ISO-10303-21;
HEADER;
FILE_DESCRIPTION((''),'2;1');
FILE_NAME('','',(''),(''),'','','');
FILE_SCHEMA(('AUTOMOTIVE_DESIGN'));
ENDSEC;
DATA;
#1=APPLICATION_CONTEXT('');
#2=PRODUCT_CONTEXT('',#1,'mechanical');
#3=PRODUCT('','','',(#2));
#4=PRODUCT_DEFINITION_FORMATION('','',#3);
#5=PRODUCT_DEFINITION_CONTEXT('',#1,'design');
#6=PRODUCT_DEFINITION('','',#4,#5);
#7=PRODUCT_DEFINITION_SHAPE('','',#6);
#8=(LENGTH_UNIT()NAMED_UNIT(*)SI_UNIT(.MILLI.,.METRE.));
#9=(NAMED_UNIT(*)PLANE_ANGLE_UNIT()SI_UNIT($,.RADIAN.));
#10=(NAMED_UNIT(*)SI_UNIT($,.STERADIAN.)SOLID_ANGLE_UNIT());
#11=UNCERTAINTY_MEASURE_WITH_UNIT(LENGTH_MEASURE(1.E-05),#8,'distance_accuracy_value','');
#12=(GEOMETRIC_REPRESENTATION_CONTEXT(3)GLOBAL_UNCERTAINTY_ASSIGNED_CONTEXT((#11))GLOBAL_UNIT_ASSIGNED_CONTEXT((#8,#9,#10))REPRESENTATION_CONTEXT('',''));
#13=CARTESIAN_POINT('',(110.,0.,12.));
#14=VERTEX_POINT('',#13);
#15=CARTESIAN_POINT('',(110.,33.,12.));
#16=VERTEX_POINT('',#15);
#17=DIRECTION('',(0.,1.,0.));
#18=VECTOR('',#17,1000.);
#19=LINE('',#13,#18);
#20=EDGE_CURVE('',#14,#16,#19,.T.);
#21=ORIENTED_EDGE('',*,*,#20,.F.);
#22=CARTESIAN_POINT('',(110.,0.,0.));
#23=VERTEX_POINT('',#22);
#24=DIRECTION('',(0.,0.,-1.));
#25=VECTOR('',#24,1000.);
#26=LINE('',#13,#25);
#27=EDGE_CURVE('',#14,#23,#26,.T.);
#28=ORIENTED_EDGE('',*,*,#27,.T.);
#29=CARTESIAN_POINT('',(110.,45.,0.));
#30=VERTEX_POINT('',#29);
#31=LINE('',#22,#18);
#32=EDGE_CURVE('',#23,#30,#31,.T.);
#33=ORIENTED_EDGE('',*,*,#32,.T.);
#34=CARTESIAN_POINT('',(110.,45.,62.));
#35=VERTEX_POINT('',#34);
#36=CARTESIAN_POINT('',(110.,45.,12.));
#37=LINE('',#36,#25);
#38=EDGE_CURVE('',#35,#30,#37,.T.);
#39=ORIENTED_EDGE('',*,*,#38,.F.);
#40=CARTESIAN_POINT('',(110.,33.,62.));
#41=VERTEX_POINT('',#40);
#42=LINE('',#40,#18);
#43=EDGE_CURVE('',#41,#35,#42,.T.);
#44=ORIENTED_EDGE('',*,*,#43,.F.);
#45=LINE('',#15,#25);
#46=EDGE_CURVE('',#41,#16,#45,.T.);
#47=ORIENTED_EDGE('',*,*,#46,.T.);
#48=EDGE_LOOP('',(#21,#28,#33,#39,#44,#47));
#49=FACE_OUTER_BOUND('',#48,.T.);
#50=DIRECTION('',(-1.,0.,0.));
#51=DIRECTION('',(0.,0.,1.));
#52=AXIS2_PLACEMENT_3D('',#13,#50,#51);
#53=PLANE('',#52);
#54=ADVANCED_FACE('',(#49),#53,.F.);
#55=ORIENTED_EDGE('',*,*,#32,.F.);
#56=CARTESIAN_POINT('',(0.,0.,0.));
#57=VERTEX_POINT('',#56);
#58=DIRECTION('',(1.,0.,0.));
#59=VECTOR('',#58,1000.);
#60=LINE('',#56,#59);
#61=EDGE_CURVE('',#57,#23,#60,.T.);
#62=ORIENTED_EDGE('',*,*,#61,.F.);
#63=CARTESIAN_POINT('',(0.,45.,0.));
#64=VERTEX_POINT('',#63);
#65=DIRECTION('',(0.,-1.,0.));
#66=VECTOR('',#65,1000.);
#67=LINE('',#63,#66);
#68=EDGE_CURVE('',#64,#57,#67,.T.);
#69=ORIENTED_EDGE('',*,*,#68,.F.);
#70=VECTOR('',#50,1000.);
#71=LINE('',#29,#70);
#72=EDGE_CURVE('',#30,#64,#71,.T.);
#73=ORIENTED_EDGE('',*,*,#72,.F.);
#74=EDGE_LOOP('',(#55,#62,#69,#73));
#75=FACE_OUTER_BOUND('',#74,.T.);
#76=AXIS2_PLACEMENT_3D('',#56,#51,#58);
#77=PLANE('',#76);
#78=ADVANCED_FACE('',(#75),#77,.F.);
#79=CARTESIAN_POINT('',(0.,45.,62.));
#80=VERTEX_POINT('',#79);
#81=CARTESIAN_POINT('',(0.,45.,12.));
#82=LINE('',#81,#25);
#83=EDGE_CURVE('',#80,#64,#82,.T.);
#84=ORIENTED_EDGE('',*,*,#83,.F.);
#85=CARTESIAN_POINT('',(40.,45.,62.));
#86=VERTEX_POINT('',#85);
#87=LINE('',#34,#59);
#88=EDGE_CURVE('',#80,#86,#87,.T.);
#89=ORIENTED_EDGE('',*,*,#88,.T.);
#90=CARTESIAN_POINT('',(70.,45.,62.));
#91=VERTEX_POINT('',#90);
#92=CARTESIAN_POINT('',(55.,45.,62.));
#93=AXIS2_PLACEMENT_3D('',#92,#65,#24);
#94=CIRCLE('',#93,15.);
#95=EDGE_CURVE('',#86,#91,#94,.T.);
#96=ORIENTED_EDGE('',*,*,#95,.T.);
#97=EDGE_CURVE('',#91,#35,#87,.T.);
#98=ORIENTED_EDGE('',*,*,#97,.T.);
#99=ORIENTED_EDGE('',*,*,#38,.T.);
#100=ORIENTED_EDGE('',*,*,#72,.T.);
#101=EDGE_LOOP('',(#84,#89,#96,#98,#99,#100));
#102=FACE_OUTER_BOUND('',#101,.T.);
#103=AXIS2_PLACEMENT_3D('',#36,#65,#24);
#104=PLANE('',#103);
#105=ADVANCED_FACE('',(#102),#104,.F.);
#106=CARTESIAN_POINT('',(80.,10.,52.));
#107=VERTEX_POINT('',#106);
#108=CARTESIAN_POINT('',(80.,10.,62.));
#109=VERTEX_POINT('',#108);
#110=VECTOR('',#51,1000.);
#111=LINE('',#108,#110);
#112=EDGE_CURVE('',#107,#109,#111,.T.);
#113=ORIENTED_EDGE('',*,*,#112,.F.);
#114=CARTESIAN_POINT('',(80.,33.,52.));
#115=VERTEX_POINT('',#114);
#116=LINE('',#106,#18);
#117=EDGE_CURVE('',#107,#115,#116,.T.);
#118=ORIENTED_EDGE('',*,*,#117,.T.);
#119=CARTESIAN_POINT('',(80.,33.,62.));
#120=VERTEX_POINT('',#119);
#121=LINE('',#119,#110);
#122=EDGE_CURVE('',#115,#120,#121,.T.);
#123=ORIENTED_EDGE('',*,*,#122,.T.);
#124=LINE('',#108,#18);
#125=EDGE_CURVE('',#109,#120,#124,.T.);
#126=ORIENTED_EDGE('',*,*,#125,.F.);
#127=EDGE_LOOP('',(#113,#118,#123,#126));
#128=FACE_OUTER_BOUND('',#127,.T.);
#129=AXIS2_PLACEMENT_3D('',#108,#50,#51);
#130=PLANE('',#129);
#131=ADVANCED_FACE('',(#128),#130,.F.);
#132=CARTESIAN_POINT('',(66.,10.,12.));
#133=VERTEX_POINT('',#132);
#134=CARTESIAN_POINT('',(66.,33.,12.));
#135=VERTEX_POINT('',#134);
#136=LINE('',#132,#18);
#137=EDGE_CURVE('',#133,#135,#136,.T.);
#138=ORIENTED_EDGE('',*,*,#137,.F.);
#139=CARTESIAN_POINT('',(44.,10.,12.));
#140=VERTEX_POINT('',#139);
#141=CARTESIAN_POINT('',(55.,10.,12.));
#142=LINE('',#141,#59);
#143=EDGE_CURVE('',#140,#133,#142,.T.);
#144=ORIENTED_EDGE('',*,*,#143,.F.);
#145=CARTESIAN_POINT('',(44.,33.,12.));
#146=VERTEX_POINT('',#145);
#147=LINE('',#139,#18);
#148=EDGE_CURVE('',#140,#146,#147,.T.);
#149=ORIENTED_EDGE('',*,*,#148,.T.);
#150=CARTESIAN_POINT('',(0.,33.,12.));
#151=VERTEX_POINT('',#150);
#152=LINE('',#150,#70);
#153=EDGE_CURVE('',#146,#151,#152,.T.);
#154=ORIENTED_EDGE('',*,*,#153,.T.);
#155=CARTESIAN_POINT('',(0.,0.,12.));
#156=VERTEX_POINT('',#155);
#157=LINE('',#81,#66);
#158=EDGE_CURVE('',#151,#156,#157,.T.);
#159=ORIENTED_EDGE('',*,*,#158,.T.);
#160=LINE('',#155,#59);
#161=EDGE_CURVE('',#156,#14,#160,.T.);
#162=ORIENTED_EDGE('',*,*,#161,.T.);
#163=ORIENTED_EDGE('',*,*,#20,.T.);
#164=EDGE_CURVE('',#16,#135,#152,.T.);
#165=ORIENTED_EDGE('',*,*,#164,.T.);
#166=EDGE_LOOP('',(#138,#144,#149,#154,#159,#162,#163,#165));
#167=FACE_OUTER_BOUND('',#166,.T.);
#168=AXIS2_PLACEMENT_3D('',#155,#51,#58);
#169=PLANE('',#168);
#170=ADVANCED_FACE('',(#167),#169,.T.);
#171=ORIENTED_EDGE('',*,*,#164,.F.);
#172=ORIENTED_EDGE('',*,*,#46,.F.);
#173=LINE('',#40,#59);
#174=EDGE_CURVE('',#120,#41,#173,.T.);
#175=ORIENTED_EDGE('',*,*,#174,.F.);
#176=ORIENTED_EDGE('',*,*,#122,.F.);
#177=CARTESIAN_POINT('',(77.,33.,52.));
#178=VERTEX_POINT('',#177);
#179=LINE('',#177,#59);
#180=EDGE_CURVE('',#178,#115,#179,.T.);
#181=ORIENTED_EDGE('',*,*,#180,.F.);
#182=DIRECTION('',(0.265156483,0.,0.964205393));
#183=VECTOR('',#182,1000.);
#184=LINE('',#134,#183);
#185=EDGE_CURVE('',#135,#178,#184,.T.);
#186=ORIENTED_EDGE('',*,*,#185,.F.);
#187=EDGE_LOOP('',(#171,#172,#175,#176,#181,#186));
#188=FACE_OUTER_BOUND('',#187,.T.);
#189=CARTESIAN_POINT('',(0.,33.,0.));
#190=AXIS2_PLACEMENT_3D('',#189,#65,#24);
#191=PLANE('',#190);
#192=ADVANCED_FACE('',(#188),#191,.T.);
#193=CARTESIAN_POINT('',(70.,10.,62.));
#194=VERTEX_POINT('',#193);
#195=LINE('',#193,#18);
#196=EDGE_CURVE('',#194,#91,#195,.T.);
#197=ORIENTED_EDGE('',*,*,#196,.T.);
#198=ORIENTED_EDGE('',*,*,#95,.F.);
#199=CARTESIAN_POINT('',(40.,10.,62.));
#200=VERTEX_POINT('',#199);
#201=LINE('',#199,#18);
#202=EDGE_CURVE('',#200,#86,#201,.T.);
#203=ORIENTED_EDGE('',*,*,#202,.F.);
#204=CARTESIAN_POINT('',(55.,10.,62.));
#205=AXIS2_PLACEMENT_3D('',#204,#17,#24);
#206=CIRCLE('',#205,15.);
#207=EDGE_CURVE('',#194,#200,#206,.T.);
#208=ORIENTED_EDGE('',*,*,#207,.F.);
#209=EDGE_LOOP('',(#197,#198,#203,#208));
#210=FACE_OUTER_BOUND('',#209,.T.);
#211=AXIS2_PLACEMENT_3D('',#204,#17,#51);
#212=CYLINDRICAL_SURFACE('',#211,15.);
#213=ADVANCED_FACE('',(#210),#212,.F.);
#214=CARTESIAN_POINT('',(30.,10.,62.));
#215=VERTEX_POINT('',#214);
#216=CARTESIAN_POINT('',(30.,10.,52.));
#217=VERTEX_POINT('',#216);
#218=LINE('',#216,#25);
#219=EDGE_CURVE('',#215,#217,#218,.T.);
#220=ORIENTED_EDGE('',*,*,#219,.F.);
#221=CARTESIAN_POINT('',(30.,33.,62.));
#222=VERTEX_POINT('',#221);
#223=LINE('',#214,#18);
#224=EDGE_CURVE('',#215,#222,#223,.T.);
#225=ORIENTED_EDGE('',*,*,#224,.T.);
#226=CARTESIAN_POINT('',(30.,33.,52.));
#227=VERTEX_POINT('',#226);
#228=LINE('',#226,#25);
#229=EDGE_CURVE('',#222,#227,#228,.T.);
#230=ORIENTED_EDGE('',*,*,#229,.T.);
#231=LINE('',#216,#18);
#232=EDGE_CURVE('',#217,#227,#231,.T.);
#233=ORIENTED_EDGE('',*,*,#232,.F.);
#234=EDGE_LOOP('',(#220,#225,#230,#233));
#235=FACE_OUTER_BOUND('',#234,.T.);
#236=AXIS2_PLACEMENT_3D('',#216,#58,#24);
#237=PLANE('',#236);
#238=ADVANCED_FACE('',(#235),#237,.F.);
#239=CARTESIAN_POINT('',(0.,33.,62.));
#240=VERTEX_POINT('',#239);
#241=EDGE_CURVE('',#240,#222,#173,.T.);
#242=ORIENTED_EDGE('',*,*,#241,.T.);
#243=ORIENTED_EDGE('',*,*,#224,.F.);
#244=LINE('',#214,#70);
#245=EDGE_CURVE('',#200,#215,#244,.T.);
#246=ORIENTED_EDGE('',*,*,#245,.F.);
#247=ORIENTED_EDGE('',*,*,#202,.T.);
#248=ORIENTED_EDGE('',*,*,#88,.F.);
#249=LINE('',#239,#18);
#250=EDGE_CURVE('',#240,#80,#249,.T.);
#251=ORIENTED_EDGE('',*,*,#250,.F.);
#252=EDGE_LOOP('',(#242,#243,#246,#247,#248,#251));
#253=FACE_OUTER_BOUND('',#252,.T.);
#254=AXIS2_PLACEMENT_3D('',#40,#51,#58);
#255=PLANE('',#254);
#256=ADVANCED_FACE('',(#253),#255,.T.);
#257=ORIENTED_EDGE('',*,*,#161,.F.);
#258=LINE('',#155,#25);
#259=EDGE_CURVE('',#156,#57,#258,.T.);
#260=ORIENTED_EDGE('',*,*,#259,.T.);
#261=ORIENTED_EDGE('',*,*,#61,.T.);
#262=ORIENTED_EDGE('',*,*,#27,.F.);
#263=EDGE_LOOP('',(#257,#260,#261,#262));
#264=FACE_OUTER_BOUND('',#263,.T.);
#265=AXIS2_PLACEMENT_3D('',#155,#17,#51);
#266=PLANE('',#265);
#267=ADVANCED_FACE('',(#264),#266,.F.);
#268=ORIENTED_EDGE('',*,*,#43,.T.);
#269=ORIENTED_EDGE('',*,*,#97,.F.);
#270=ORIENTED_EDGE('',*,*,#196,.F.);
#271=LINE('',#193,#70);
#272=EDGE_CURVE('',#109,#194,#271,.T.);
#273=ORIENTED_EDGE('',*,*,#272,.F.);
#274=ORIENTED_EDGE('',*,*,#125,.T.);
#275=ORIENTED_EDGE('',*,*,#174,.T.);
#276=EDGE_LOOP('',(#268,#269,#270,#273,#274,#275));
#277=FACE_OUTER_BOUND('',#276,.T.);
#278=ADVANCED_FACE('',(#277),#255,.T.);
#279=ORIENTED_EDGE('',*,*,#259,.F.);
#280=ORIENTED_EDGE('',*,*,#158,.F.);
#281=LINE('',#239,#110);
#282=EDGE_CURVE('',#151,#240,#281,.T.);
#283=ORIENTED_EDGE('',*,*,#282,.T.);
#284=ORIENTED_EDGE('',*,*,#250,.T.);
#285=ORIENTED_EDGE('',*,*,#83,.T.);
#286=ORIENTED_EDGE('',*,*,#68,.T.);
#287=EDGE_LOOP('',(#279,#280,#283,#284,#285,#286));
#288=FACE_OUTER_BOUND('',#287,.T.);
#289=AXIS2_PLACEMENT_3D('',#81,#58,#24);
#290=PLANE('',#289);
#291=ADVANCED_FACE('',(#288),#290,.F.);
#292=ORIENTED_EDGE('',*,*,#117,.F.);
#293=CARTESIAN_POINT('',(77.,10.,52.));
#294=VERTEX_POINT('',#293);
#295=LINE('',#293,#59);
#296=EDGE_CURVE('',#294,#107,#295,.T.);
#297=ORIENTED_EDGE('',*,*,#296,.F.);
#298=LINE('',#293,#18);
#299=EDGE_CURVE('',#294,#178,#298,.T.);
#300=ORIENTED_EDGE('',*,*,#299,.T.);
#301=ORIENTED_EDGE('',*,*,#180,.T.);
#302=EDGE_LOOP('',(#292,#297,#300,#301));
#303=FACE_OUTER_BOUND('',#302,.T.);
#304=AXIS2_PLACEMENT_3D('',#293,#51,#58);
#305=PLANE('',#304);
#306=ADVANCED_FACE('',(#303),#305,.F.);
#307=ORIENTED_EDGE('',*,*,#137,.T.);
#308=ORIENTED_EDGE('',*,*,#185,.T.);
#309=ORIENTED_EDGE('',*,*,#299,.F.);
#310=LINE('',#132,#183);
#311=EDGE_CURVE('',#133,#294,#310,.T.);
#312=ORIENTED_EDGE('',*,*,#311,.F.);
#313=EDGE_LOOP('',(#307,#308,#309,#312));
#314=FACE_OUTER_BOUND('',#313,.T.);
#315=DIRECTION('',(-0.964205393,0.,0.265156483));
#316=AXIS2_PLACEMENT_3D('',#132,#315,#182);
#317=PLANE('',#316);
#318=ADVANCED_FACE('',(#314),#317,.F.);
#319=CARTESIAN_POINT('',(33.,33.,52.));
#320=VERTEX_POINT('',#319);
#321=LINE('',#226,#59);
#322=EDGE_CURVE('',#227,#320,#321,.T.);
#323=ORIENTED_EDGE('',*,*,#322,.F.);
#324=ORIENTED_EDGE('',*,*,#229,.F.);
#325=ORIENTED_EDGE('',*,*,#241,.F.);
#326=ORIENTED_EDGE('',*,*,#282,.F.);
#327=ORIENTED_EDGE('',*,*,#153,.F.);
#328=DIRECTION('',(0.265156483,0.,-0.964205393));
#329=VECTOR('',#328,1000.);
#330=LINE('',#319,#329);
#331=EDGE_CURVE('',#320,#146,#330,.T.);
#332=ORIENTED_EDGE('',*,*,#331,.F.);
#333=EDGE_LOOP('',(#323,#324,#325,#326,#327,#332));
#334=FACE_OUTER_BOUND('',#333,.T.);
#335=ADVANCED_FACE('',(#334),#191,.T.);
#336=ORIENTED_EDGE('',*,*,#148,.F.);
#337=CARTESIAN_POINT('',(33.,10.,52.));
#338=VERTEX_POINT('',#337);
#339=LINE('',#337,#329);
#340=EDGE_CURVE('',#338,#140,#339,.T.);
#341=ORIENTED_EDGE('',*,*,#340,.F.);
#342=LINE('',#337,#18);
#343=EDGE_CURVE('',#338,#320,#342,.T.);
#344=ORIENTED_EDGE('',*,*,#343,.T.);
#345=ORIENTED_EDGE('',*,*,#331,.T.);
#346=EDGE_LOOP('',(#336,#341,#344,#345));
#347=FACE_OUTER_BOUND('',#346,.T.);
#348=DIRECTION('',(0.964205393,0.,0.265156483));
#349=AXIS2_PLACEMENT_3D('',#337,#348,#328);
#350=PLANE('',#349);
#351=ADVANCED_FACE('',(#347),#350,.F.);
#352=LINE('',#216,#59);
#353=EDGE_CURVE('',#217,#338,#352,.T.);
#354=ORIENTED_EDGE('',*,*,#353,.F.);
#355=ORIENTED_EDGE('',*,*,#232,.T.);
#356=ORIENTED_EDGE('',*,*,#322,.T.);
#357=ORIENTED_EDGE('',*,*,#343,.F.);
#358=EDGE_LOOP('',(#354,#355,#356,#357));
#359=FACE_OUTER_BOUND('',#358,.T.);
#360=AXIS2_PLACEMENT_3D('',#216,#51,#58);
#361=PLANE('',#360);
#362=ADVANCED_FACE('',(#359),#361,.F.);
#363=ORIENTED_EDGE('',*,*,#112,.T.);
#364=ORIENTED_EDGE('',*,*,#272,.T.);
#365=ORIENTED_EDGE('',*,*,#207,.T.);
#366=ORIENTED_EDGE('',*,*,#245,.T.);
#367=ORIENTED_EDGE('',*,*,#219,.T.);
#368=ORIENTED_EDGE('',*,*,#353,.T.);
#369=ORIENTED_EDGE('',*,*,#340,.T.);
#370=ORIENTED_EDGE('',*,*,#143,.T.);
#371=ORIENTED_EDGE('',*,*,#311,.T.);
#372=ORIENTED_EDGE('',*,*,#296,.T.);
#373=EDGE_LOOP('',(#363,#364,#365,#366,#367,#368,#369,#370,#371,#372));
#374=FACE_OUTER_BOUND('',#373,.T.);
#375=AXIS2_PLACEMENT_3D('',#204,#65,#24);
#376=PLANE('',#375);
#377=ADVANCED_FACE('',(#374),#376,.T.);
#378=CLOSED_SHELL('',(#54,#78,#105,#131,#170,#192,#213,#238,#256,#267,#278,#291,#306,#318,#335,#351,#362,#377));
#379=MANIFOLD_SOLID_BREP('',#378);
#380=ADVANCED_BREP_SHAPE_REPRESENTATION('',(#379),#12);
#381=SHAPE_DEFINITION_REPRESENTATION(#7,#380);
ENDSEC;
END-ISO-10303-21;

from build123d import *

# Parameters (mm, degrees)
BASE_PLATE_SKETCH_W          = 110
BASE_PLATE_SKETCH_H          = 45
BASE_PLATE_DEPTH             = 12
SECOND_BLOCK_SKETCH_W        = 110
SECOND_BLOCK_SKETCH_H        = 50
SECOND_BLOCK_DEPTH           = 12
LEG_PROFILE_BOSS_DEPTH       = 23
SEMICIRCULAR_START           = -12
SEMICIRCULAR_NOTCH_CUT_DEPTH = 12


with BuildPart() as part:
    # Base Plate Sketch → Base Plate (new body)
    with BuildSketch(Plane.XY):
        with Locations((55, 22.5)):
            Rectangle(BASE_PLATE_SKETCH_W, BASE_PLATE_SKETCH_H)
    extrude(amount=BASE_PLATE_DEPTH)

    # Second Block Sketch → Second Block (add)
    with BuildSketch(Plane(origin=(0, 45, 0), x_dir=(1, 0, 0), z_dir=(0, 1, 0))):
        with Locations((55, -37)):
            Rectangle(SECOND_BLOCK_SKETCH_W, SECOND_BLOCK_SKETCH_H)
    extrude(amount=-SECOND_BLOCK_DEPTH)

    # Leg Profile Sketch → Leg Profile Boss (add)
    with BuildSketch(Plane.XZ.offset(-33)):
        with BuildLine():
            Line((80, 62), (80, 52))
            Line((80, 52), (77, 52))
            Line((77, 52), (66, 12))
            Line((66, 12), (55, 12))
            Line((55, 12), (44, 12))
            Line((44, 12), (33, 52))
            Line((33, 52), (30, 52))
            Line((30, 52), (30, 62))
            Line((30, 62), (40, 62))
            ThreePointArc((40, 62), (55, 47), (70, 62))
            Line((70, 62), (80, 62))
        make_face()
    extrude(amount=LEG_PROFILE_BOSS_DEPTH)

    # Semicircular Notch Sketch → Semicircular Notch Cut (cut)
    with BuildSketch(Plane.XZ.offset(-33).offset(SEMICIRCULAR_START)):
        with BuildLine():
            Line((40, 62), (70, 62))
            ThreePointArc((70, 62), (55, 47), (40, 62))
        make_face()
    extrude(amount=SEMICIRCULAR_NOTCH_CUT_DEPTH, mode=Mode.SUBTRACT)


solid = part.part
